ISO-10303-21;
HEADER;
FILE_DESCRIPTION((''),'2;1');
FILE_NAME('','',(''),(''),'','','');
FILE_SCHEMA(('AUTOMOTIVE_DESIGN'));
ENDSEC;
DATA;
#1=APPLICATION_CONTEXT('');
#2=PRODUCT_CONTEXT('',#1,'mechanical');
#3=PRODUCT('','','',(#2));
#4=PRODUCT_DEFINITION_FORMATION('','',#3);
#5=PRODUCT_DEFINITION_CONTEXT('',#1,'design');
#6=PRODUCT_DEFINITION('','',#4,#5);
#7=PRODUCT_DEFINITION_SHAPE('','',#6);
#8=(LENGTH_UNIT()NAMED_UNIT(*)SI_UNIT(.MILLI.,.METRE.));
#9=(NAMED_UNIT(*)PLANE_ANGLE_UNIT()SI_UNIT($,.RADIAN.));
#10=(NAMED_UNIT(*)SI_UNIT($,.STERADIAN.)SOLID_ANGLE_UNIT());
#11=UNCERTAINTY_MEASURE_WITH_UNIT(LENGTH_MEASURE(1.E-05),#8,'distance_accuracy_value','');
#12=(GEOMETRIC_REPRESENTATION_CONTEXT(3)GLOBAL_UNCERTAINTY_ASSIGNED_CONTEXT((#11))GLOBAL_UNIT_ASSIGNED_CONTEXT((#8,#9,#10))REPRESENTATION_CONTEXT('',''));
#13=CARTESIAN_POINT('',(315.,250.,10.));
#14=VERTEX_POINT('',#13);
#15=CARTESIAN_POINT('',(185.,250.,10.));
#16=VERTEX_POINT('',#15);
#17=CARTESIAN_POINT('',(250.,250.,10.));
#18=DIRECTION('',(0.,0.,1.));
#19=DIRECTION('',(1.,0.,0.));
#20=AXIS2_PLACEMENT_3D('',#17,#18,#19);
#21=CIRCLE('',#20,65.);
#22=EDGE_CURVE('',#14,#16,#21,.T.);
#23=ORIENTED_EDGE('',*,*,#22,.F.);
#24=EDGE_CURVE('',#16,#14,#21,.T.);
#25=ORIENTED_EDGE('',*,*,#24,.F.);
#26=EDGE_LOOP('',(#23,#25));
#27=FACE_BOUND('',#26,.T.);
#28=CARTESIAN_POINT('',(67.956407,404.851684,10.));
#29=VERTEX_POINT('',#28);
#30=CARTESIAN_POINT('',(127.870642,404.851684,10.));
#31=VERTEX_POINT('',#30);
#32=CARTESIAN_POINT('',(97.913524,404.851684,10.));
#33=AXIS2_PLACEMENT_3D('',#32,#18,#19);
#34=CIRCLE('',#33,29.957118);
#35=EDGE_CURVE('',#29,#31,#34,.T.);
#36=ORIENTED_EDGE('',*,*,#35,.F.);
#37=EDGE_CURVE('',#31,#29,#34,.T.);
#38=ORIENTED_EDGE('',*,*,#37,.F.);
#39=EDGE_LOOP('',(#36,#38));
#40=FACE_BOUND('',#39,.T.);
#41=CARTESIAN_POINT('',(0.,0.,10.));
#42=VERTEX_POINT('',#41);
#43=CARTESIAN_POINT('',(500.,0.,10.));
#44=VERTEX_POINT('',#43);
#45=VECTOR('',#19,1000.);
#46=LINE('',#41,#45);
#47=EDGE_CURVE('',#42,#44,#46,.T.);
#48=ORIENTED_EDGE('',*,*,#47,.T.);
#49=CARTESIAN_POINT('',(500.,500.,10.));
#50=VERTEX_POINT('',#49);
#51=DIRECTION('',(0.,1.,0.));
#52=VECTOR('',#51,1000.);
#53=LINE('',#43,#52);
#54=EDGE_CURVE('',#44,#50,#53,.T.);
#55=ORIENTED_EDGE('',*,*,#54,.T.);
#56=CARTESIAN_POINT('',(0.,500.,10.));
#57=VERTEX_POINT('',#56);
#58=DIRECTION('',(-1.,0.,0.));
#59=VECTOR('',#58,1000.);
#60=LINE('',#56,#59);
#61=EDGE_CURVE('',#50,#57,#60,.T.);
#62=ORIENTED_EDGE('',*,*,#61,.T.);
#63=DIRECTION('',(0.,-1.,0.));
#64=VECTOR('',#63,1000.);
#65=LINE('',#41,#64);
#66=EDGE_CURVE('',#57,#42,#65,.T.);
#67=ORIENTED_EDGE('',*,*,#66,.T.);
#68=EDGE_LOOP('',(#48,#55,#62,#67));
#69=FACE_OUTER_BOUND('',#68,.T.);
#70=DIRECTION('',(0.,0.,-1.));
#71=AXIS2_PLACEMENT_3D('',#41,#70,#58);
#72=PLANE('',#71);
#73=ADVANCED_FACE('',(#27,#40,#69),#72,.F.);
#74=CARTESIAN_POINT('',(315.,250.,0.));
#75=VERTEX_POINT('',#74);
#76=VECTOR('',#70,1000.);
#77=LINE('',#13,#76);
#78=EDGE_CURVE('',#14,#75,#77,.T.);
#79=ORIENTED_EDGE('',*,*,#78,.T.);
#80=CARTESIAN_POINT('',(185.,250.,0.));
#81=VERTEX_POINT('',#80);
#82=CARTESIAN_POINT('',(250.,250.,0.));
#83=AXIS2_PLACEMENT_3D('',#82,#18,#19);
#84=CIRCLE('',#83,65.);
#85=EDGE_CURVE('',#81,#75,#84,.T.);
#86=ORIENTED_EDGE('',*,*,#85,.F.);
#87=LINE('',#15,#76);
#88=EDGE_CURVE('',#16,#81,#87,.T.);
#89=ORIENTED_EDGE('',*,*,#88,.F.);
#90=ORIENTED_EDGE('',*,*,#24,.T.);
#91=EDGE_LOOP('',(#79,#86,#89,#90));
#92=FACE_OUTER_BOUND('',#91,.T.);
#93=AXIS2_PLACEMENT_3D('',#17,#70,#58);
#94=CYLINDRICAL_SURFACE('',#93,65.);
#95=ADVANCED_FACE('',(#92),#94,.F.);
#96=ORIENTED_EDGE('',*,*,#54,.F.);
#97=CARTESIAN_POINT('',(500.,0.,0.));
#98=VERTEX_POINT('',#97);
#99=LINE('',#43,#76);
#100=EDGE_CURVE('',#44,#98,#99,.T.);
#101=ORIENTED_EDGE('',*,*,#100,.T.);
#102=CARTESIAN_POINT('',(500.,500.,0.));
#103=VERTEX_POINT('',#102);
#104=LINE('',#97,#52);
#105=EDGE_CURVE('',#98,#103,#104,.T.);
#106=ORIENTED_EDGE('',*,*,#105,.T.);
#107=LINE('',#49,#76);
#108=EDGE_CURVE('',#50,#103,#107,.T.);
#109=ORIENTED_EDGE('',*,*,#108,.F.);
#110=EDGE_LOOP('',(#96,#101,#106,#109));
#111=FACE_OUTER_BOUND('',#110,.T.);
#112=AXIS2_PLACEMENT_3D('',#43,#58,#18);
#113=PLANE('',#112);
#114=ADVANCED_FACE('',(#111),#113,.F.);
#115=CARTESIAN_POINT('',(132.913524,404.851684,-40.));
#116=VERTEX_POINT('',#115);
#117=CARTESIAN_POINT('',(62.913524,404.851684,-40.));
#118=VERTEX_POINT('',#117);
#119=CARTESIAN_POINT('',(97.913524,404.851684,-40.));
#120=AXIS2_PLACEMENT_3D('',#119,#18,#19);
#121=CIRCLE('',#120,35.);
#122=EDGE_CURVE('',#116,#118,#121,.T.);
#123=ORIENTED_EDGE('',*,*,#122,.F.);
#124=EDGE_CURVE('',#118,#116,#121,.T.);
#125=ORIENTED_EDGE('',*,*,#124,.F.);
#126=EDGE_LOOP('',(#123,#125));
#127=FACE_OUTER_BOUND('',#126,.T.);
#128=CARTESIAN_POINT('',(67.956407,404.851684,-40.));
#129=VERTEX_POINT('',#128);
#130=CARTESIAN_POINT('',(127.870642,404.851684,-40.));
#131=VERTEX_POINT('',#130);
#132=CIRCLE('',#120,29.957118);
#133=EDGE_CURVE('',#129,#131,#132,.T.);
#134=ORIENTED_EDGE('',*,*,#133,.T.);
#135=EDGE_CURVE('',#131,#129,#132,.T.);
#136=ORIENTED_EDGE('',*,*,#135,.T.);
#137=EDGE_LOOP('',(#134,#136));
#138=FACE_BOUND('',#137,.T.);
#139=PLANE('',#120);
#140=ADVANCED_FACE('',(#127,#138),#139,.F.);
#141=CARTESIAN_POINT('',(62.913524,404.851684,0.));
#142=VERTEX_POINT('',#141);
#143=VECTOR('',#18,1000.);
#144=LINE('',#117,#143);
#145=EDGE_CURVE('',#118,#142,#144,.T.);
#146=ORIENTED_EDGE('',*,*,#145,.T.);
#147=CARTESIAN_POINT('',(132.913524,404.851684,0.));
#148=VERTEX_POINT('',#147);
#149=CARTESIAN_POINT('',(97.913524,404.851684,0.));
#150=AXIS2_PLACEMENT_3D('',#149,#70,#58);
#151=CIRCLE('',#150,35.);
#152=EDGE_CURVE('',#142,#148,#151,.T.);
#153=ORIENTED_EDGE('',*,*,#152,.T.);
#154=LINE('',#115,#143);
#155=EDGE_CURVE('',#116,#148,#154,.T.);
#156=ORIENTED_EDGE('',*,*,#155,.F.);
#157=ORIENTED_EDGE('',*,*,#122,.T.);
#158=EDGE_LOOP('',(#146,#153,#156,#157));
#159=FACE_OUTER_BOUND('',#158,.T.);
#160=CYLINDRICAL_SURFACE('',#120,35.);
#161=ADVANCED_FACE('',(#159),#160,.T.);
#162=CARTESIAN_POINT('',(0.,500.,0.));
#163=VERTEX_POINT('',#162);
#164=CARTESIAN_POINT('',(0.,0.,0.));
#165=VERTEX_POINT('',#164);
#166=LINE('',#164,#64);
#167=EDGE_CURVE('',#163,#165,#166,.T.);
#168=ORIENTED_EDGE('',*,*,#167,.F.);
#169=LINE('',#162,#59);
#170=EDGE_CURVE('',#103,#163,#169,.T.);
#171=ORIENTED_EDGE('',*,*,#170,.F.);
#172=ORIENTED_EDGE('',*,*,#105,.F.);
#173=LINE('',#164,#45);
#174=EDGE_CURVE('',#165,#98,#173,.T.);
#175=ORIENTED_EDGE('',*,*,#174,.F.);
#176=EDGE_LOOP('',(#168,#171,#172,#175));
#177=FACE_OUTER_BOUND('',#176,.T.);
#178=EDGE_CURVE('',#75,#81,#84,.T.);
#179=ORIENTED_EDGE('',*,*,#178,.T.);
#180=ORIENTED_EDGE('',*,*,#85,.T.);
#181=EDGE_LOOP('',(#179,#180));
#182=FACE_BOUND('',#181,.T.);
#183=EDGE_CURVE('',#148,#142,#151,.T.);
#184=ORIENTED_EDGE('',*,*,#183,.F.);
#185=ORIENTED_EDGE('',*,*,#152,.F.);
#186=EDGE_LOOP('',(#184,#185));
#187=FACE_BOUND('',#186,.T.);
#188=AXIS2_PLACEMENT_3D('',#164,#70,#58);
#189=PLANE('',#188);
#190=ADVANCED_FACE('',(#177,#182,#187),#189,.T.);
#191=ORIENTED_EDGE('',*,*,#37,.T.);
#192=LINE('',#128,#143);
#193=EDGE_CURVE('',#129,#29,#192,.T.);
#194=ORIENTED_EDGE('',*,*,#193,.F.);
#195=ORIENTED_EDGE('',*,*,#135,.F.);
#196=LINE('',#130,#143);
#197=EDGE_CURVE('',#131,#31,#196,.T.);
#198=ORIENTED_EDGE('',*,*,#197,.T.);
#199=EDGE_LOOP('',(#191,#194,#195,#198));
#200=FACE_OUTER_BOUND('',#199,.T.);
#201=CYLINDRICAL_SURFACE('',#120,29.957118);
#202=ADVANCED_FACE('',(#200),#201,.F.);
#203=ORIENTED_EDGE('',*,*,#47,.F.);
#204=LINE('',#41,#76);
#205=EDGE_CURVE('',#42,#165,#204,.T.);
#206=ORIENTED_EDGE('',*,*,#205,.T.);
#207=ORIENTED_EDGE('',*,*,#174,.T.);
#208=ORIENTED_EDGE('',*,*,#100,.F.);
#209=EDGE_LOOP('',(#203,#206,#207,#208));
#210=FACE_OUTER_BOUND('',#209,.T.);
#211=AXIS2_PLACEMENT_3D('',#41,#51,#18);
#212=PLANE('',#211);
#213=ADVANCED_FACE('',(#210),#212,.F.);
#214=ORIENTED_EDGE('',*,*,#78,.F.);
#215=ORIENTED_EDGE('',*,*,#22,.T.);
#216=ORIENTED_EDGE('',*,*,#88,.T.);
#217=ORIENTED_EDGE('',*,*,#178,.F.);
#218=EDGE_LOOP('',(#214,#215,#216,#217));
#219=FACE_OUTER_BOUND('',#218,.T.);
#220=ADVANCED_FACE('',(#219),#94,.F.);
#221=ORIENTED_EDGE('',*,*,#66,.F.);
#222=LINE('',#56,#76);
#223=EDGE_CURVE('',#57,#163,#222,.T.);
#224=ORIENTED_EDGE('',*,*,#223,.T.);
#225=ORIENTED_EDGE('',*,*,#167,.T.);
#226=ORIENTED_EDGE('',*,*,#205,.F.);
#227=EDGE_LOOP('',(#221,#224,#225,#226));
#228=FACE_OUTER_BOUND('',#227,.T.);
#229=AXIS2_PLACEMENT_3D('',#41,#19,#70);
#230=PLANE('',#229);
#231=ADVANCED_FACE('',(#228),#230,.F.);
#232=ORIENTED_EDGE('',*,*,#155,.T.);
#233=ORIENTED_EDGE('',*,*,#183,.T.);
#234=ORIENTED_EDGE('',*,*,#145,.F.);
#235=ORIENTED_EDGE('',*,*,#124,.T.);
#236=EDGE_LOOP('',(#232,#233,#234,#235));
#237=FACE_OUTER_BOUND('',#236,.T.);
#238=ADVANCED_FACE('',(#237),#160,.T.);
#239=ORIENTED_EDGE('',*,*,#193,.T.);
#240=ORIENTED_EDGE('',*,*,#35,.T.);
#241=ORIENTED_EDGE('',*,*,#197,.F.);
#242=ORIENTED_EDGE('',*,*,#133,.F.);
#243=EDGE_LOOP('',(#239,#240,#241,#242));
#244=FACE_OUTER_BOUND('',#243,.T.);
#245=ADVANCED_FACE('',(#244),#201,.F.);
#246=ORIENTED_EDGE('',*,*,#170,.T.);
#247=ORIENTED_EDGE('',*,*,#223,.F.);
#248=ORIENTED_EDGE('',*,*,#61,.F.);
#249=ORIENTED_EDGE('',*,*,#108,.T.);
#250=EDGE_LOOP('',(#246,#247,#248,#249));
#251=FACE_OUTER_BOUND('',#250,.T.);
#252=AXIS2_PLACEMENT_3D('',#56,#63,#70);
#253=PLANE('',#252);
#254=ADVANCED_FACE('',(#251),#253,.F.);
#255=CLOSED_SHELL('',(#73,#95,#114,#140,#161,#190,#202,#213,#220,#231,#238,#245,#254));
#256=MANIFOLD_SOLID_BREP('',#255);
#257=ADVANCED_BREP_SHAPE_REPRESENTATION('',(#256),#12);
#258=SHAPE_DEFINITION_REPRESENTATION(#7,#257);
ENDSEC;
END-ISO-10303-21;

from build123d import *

# Parameters (mm, degrees)
SKETCH1_W           = 500
SKETCH1_H           = 500
SKETCH1_R           = 65
SKETCH1_R_2         = 30
BOSS_EXTRUDE1_DEPTH = 10
SKETCH2_R           = 35
SKETCH2_R_2         = 29.957117648
BOSS_EXTRUDE2_DEPTH = 50


with BuildPart() as part:
    # Sketch1 → Boss-Extrude1 (new body)
    with BuildSketch(Plane.XY):
        with Locations((250, 250)):
            Rectangle(SKETCH1_W, SKETCH1_H)
        with Locations((250, 250)):
            Circle(SKETCH1_R, mode=Mode.SUBTRACT)
        with Locations((97.913524384, 404.851684263)):
            Circle(SKETCH1_R_2, mode=Mode.SUBTRACT)
    extrude(amount=BOSS_EXTRUDE1_DEPTH)

    # Sketch2 → Boss-Extrude2 (add)
    with BuildSketch(Plane.XY.offset(10)):
        with Locations((97.913524384, 404.851684263)):
            Circle(SKETCH2_R)
        with Locations((97.913524384, 404.851684263)):
            Circle(SKETCH2_R_2, mode=Mode.SUBTRACT)
    extrude(amount=-BOSS_EXTRUDE2_DEPTH)


solid = part.part
